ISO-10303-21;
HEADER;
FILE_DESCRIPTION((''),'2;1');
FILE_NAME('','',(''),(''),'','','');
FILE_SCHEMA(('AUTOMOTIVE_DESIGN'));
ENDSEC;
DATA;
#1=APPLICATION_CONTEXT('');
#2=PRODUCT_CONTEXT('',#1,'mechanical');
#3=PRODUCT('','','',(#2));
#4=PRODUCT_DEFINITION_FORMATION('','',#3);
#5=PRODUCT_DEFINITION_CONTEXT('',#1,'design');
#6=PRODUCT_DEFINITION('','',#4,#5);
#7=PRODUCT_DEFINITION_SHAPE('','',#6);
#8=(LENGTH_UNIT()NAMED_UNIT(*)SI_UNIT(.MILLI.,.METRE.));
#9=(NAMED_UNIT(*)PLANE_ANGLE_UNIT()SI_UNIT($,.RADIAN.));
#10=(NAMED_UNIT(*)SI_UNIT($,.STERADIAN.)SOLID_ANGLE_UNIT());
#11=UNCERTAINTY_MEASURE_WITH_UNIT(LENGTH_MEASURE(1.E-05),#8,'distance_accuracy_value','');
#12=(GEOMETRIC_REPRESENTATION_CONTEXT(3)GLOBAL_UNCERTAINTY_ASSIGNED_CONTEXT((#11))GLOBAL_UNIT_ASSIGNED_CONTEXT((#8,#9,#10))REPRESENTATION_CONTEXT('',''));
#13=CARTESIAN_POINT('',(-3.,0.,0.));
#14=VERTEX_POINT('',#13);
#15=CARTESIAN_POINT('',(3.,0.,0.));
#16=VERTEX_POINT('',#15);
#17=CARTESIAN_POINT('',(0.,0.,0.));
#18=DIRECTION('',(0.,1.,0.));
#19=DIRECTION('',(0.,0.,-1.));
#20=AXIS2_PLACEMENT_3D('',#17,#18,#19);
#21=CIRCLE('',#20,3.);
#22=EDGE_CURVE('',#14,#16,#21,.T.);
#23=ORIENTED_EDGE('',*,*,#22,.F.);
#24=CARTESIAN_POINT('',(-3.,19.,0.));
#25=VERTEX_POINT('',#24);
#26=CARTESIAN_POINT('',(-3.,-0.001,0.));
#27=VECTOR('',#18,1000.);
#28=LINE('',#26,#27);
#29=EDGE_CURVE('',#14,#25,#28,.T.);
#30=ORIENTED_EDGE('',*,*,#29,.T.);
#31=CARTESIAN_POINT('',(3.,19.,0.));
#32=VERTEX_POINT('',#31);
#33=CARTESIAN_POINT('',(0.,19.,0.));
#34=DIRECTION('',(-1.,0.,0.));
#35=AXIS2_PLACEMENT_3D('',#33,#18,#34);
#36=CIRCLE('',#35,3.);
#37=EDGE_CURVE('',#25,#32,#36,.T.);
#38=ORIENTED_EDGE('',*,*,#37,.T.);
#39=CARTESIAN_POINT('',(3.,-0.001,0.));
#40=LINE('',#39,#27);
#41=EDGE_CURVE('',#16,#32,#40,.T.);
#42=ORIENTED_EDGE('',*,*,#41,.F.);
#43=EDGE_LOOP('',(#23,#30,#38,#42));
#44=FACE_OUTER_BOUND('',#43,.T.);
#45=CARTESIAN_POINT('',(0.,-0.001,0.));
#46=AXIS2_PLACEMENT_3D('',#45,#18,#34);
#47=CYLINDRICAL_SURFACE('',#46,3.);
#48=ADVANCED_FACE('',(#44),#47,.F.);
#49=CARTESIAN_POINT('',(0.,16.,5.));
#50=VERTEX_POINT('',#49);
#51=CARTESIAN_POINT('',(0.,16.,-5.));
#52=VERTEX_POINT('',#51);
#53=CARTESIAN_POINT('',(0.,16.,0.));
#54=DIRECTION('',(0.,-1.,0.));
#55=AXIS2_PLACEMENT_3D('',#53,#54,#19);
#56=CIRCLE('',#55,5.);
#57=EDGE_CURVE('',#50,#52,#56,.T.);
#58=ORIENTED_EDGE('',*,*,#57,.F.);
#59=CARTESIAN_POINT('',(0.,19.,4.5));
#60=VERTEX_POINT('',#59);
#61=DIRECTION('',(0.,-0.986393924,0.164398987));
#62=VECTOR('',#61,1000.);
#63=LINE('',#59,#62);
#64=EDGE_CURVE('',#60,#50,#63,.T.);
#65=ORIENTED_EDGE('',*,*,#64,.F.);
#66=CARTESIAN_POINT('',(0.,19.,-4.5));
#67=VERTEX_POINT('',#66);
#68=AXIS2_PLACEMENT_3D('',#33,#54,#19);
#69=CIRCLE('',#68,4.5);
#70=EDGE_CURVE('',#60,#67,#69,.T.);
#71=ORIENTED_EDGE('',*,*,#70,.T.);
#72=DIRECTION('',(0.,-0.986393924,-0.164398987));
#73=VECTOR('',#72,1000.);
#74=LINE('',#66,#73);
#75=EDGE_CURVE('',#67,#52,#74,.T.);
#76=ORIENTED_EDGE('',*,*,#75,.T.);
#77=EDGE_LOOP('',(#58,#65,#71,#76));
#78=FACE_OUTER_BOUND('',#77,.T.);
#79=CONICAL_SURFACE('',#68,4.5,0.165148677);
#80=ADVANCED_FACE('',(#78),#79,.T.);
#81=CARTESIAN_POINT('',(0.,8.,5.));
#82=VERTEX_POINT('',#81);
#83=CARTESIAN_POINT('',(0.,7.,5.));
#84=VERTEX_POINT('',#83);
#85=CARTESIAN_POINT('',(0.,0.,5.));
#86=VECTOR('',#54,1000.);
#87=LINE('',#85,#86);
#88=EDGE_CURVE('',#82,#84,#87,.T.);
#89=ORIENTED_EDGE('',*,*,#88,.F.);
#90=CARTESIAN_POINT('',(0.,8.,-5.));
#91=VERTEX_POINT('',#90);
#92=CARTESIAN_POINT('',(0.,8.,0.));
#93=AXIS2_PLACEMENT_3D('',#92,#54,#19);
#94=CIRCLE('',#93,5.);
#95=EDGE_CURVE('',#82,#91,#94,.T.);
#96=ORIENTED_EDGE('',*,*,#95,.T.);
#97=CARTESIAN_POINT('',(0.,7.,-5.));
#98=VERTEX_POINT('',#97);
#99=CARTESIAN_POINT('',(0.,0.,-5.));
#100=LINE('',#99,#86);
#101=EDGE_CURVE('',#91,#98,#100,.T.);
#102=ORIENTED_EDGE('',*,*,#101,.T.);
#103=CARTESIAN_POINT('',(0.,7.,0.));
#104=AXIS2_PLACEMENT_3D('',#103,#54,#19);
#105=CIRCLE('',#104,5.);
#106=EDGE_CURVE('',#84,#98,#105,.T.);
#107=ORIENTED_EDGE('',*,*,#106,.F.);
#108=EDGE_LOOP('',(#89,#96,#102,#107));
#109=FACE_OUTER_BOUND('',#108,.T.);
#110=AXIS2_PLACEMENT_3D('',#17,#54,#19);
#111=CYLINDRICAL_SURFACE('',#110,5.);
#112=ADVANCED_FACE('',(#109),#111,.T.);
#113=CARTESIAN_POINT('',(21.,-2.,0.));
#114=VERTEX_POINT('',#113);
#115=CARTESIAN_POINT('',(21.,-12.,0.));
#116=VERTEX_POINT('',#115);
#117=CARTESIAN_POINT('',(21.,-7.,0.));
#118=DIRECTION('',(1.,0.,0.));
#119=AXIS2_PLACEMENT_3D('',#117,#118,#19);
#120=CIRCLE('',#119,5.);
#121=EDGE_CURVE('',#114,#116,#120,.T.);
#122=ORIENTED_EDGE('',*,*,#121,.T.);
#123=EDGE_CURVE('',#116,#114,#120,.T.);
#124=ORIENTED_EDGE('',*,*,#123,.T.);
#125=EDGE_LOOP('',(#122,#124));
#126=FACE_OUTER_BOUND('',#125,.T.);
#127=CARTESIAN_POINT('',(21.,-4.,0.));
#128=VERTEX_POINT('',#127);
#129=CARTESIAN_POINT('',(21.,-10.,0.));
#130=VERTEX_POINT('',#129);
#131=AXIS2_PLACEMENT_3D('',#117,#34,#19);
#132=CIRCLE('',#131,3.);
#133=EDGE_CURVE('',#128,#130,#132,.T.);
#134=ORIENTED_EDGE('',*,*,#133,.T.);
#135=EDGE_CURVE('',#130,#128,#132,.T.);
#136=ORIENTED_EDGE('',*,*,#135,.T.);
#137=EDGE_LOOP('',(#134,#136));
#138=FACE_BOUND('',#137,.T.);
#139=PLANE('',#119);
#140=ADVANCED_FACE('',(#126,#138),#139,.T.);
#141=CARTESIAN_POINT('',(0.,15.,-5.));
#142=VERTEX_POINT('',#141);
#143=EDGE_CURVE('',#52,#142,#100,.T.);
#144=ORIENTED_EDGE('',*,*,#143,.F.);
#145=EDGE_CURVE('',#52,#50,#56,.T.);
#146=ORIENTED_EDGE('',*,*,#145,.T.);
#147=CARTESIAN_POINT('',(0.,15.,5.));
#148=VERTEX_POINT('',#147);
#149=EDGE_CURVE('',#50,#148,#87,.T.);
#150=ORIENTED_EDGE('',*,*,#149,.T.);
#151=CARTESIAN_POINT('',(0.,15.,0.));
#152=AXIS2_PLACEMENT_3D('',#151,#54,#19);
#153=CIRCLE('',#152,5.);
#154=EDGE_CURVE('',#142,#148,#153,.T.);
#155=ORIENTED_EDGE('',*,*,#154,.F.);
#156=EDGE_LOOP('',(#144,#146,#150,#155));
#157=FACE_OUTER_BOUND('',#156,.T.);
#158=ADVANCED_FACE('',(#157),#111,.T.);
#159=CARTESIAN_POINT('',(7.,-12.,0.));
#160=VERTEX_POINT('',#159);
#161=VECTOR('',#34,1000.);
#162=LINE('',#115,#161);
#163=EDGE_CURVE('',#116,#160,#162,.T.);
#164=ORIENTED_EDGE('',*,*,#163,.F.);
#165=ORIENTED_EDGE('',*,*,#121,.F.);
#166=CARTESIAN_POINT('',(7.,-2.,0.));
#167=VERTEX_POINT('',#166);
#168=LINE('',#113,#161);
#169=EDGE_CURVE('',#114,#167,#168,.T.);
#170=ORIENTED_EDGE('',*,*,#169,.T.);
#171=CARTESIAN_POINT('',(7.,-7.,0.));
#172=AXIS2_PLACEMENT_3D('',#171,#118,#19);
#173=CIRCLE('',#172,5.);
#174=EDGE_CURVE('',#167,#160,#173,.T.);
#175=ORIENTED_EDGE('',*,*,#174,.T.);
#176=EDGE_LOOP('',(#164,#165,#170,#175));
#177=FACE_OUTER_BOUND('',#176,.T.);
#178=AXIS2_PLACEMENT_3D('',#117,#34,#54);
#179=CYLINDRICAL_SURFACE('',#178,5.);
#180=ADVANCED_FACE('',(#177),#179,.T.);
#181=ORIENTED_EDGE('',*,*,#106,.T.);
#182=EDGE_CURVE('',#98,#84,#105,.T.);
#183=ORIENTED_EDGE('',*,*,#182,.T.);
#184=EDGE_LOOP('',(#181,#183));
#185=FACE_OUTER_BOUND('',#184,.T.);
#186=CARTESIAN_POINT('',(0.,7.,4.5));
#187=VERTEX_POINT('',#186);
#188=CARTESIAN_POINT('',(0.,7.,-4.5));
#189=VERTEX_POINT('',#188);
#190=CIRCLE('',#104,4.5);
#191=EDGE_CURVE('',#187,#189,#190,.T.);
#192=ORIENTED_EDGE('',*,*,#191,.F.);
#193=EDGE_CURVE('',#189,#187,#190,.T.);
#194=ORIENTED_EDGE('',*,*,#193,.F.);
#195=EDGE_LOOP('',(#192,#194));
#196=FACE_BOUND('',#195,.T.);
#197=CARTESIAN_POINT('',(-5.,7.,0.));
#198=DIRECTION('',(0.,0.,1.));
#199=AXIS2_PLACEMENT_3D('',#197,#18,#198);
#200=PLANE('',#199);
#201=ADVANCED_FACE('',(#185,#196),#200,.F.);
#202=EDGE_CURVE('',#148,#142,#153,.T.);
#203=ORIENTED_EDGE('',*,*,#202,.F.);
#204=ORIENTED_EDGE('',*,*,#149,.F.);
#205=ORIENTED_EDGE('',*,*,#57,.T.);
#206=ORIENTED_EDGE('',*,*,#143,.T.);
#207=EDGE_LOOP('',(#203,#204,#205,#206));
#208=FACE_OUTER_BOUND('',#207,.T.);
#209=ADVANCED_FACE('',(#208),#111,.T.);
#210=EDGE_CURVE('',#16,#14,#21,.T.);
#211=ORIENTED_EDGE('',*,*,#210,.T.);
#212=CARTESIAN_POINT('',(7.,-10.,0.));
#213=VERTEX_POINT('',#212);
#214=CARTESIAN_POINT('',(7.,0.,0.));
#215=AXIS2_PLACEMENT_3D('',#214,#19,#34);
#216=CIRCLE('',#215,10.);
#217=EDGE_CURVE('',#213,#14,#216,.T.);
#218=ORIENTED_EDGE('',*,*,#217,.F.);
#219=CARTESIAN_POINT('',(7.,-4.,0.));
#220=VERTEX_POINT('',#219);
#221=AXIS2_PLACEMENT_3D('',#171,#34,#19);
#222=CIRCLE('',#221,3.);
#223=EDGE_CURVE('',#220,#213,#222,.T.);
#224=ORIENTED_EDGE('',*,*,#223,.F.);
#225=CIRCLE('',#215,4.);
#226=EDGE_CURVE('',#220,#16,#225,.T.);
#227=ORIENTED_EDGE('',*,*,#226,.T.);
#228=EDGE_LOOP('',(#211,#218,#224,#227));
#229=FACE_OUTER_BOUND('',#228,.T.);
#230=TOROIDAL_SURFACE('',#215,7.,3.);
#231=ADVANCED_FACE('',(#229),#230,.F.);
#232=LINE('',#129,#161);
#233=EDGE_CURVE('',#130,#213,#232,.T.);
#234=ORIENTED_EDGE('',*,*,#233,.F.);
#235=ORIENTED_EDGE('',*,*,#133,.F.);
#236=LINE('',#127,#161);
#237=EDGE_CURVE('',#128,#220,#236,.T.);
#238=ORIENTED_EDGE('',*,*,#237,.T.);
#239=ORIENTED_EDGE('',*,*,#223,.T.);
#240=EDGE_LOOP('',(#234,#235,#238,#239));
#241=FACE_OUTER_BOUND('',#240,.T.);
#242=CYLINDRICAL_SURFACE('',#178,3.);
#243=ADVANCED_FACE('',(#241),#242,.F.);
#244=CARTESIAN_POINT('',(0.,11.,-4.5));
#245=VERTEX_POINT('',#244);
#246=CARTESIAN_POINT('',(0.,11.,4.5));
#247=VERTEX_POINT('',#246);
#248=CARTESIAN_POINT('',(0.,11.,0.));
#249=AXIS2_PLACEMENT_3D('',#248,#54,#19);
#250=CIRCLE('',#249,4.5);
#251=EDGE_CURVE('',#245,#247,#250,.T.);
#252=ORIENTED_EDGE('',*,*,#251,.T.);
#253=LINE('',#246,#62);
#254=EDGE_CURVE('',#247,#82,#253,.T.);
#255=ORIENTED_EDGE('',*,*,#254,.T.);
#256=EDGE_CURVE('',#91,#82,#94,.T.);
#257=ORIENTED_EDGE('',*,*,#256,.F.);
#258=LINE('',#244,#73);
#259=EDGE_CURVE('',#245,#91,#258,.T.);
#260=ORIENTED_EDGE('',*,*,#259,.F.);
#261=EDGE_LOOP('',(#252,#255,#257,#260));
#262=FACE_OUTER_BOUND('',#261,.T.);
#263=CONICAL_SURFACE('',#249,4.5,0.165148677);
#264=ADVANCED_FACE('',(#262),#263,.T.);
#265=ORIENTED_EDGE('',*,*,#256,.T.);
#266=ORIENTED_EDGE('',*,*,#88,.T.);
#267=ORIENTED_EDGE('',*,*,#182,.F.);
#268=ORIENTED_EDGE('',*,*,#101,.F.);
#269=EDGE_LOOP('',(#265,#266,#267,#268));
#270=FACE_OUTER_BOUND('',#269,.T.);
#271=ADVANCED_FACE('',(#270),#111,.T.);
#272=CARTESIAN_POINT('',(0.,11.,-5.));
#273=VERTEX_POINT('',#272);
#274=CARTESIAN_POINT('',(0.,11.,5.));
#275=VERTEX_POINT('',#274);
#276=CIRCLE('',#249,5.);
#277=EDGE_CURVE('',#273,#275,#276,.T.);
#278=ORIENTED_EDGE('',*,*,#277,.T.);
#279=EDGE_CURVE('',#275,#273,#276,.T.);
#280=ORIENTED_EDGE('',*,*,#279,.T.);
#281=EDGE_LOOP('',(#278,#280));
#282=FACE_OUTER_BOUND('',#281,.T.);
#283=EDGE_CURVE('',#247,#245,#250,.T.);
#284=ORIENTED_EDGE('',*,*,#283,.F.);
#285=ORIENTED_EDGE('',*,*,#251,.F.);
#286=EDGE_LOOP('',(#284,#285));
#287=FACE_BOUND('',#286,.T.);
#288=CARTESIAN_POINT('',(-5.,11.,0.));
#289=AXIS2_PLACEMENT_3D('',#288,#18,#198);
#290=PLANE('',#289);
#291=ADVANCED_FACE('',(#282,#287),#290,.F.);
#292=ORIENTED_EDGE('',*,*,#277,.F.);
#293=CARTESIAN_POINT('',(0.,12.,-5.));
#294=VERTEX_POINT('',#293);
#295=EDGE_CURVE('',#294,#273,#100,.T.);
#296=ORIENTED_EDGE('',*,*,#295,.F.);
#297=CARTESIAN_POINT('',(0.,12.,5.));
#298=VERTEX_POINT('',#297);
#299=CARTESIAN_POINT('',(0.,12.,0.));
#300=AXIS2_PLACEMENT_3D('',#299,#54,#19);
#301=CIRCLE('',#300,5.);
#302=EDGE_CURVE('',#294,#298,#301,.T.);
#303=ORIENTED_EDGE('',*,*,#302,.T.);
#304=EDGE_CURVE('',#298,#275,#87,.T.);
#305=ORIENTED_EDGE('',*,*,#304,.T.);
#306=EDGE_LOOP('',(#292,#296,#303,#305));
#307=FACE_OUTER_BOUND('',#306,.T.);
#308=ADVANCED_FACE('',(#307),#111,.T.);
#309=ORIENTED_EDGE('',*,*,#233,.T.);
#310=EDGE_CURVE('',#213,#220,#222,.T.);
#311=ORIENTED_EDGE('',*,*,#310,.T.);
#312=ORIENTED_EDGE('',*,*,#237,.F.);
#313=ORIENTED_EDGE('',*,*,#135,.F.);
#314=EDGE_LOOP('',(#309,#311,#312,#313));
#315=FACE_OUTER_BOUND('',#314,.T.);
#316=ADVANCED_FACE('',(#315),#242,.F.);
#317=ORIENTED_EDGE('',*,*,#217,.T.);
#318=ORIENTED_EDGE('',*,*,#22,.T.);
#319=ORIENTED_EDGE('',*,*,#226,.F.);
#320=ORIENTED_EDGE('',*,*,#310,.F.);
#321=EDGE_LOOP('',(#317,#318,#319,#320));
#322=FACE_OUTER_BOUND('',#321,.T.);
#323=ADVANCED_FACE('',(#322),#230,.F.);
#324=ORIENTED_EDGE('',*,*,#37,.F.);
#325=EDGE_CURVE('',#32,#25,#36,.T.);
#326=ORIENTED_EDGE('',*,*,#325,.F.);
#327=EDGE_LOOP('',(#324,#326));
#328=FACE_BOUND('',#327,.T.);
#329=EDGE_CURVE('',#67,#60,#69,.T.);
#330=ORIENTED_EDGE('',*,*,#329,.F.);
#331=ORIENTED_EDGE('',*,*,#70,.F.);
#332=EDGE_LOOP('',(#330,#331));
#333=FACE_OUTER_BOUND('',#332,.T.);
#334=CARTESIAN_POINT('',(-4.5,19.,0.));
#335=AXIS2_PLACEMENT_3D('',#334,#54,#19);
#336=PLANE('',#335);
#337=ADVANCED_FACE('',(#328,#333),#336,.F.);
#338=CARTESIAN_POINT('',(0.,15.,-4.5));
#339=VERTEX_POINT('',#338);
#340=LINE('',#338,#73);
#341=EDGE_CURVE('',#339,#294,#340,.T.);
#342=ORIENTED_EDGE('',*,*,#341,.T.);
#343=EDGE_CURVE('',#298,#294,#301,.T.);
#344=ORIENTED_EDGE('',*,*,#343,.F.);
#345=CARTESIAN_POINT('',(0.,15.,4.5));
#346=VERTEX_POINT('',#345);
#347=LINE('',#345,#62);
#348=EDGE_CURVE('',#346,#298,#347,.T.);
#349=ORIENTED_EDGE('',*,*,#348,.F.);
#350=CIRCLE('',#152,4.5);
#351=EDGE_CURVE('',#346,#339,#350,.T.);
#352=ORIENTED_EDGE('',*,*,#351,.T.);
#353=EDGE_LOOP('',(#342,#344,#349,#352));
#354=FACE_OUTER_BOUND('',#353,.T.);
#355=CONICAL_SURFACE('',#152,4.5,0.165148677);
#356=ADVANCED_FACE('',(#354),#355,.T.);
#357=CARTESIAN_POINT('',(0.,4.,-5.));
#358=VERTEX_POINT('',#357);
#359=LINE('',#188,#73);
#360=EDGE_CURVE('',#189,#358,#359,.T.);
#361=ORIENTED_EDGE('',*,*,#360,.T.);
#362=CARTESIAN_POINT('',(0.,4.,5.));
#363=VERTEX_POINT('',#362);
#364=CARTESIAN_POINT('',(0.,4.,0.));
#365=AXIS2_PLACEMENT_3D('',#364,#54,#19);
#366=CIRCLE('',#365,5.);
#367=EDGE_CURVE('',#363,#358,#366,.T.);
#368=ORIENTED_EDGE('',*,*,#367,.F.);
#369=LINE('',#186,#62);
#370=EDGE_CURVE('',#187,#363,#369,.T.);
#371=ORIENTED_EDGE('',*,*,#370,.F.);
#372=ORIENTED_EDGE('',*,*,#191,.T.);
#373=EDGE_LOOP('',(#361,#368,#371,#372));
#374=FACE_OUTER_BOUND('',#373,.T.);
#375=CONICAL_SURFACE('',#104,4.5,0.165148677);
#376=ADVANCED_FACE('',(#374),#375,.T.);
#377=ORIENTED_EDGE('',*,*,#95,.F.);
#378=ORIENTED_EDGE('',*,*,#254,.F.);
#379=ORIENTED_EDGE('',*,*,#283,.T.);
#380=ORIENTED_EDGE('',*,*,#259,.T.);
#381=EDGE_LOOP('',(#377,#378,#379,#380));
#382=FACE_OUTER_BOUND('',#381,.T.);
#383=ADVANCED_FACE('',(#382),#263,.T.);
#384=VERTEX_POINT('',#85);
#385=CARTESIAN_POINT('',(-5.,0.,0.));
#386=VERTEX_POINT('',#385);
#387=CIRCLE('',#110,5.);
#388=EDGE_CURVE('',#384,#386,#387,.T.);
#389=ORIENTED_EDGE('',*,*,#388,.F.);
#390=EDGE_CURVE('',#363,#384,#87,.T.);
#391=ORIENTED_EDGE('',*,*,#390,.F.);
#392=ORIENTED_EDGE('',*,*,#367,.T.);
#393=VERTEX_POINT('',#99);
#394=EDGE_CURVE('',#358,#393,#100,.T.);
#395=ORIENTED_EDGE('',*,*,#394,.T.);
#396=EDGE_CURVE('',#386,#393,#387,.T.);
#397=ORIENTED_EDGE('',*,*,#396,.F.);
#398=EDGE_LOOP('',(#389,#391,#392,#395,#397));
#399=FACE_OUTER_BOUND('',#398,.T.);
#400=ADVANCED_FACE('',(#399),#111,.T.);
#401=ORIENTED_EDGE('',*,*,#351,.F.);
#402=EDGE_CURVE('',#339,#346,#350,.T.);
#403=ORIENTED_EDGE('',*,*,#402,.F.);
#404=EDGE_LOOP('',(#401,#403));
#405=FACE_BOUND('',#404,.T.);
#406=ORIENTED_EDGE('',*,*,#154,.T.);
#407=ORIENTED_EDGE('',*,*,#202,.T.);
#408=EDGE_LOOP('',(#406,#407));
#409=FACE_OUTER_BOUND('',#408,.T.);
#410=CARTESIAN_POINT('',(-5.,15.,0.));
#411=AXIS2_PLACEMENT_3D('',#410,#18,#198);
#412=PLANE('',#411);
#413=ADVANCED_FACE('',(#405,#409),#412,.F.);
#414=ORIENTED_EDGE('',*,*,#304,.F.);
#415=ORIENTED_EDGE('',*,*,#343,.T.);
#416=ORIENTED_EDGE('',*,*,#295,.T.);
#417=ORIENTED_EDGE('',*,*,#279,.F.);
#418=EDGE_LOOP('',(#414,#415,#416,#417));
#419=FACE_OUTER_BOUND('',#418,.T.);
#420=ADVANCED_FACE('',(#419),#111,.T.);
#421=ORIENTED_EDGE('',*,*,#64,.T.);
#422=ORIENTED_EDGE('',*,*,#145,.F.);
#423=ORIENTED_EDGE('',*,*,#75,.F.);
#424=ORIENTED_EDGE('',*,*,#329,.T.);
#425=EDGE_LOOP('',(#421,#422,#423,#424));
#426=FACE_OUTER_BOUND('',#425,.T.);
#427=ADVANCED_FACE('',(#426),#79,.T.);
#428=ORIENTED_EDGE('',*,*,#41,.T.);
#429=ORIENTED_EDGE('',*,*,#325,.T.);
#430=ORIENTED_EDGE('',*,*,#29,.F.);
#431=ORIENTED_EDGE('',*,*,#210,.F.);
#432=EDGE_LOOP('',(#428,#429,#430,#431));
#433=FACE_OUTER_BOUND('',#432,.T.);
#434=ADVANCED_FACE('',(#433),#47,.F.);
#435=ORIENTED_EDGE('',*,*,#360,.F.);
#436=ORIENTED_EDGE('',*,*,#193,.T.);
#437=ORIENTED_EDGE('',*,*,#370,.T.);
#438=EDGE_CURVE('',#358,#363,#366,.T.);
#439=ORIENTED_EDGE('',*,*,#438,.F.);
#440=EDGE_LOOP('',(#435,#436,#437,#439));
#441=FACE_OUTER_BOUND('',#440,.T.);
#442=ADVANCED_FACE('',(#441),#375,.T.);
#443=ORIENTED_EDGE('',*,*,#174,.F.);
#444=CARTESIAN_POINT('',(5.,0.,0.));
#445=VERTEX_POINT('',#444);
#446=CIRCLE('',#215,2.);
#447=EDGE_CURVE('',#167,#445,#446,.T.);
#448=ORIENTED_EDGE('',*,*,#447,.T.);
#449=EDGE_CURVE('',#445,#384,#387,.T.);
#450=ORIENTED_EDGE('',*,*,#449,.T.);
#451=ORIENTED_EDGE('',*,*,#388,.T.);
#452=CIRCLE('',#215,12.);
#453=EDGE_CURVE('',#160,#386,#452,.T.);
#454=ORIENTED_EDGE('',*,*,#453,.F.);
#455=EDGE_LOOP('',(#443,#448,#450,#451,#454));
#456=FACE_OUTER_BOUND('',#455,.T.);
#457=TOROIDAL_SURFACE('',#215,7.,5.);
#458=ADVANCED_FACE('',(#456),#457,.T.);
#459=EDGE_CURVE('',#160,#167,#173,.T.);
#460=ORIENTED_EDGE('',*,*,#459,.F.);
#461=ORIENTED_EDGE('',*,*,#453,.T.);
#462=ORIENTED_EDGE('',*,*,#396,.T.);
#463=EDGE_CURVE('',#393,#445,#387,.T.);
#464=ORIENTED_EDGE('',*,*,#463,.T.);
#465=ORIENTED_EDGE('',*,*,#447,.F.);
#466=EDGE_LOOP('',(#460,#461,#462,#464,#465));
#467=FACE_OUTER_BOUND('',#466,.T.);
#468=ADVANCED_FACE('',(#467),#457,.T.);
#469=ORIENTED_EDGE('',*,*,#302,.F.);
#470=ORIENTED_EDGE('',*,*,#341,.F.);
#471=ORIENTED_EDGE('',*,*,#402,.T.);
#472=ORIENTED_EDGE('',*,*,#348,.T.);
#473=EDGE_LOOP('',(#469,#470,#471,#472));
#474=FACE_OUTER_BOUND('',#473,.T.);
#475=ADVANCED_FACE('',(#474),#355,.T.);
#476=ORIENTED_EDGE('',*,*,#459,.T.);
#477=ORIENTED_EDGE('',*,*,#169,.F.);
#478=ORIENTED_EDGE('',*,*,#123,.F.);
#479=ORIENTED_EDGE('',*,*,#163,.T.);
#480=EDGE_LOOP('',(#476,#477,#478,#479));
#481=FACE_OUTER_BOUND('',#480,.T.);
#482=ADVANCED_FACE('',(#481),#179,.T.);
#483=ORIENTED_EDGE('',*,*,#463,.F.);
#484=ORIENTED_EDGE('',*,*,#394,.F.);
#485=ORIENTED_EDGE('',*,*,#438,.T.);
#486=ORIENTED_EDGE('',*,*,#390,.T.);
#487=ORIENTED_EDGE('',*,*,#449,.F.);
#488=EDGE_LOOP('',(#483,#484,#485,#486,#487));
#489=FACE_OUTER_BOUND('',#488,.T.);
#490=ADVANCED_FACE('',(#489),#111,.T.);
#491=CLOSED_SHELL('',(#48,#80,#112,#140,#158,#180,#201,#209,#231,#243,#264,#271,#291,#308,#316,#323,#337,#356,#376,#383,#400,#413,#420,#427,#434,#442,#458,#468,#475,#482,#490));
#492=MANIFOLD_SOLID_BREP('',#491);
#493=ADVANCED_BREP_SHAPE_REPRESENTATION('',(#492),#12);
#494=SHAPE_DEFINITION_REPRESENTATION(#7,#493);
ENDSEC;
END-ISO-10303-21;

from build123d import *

# Parameters (mm, degrees)
CUT_EXTRUDE_1_REACH = 22.273
SKETCH_4_R          = 3
SKETCH_6_R          = 5
SKETCH_6_R_2        = 3


with BuildPart() as part:
    # 草图1 → 旋转1 (revolve)
    with BuildSketch(Plane.XY, mode=Mode.PRIVATE) as revolve_1_sk:
        Polygon((-5, 4), (-4.5, 7), (-5, 7), (-5, 8), (-4.5, 11), (-5, 11), (-5, 12), (-4.5, 15), (-5, 15), (-5, 16), (-4.5, 19), (0, 19), (0, 0), (-5, 0), align=None)
    revolve(revolve_1_sk.sketch.rotate(Axis((0, 0, 0), (0, 1, 0)), 270), axis=Axis((0, 0, 0), (0, 1, 0)))

    # 草图4 → 切除-拉伸1 (cut, up to next)
    with BuildSketch(Plane(origin=(0, 19, 0), x_dir=(1, 0, 0), z_dir=(0, 1, 0)), mode=Mode.PRIVATE) as cut_extrude_1_sk1:
        with Locations(Location((0, 0, 0), (0, 0, 180))):
            Circle(SKETCH_4_R)
    cut_extrude_1_tool1 = extrude(cut_extrude_1_sk1.sketch, amount=-CUT_EXTRUDE_1_REACH, mode=Mode.PRIVATE) & part.part
    add(cut_extrude_1_tool1.solids().sort_by_distance((0, 19, 0))[0], mode=Mode.SUBTRACT)

    # 扫描1: sweep along a path in 草图5
    with BuildLine(Plane.XY) as sweep_1_path:
        Line((21, -7), (7, -7))
        ThreePointArc((7, -7), (2.050252532, -4.949747468), (0, 0))
    # 草图6 → 扫描1 (sweep)
    with BuildSketch(Plane.XZ):
        Circle(SKETCH_6_R)
        Circle(SKETCH_6_R_2, mode=Mode.SUBTRACT)
    sweep(path=sweep_1_path.line)


solid = part.part
